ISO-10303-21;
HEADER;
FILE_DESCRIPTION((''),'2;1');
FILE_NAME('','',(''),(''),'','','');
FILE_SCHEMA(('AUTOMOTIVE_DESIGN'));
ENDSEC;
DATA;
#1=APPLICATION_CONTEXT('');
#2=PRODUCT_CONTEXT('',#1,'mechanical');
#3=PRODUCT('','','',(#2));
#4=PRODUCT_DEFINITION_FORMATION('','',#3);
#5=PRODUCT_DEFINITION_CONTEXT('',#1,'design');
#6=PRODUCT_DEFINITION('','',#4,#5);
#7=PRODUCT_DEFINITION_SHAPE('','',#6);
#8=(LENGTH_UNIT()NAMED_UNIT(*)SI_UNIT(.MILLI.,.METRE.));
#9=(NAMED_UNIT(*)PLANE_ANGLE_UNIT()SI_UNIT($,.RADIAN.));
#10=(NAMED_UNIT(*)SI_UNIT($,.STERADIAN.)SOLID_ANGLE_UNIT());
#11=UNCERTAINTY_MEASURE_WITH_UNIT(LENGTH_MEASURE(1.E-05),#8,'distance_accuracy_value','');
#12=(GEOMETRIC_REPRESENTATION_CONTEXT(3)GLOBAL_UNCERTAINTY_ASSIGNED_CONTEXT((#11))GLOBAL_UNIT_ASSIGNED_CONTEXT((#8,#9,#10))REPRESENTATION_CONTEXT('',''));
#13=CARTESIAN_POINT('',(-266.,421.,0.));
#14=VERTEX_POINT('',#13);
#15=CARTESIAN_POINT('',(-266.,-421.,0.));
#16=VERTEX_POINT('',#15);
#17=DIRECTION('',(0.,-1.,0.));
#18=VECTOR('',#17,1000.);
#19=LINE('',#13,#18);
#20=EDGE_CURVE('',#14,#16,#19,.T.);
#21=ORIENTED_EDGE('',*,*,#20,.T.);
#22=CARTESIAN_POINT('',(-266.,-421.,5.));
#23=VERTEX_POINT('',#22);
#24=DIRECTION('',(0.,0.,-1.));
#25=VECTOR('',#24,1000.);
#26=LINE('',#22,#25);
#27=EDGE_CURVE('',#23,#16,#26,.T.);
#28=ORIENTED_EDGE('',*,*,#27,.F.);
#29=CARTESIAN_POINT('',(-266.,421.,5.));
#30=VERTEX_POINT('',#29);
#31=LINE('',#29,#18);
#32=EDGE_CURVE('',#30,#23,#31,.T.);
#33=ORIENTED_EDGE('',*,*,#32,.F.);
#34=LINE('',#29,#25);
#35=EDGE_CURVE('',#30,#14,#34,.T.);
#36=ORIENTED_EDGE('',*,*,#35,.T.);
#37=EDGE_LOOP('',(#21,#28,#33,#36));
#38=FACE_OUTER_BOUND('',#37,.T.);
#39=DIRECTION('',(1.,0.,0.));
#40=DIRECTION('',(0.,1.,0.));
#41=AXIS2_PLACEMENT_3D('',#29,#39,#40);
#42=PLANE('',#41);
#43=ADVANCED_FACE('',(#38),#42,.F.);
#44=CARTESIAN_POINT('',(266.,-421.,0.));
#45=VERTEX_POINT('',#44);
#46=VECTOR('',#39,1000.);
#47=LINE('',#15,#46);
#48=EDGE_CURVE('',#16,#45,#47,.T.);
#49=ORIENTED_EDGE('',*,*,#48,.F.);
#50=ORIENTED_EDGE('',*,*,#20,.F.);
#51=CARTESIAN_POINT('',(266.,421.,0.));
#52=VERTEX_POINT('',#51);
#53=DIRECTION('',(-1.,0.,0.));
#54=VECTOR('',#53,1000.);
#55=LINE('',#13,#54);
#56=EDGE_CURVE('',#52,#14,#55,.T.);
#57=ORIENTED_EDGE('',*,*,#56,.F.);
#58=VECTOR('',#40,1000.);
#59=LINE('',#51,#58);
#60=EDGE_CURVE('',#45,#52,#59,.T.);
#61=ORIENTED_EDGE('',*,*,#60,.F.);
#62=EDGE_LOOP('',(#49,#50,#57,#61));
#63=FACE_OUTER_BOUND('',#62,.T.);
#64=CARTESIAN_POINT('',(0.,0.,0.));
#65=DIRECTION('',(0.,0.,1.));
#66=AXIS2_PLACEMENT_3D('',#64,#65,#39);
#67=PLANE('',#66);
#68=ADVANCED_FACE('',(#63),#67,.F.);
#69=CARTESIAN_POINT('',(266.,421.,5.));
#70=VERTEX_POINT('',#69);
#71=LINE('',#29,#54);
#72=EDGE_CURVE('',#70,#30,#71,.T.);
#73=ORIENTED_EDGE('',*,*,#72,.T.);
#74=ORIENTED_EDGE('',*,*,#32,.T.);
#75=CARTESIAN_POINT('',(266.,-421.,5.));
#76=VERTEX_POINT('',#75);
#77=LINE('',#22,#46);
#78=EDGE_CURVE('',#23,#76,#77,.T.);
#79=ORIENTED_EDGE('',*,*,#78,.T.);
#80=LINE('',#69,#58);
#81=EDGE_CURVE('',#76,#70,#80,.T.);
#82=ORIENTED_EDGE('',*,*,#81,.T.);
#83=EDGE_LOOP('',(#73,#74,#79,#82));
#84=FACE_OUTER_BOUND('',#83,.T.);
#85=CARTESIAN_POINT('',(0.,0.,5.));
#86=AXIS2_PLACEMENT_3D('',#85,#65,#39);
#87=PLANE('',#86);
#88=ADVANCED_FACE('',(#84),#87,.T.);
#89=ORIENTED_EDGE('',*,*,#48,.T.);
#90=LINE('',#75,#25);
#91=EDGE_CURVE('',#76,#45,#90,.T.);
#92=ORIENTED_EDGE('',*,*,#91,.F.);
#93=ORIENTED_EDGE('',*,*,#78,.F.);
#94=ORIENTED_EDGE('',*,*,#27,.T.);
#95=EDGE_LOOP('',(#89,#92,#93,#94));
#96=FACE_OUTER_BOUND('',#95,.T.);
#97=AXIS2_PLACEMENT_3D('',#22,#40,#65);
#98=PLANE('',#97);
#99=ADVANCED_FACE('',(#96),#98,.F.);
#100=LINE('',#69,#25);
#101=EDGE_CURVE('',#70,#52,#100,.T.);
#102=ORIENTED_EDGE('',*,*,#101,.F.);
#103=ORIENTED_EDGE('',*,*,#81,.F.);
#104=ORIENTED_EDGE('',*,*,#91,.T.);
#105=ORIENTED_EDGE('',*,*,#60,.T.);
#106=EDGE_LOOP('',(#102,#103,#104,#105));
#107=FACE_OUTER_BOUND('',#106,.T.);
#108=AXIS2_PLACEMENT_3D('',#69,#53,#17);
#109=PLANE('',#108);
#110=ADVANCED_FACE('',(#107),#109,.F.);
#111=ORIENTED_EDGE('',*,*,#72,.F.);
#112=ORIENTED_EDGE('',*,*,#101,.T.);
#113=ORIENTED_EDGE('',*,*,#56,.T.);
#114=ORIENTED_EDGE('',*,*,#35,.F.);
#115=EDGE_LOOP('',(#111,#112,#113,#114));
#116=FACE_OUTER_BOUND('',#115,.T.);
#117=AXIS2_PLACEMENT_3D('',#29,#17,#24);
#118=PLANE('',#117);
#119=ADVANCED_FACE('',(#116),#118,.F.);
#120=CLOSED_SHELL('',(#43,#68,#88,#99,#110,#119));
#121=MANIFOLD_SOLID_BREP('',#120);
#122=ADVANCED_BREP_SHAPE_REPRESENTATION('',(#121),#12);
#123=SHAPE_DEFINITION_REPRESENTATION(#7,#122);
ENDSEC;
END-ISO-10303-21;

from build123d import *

# Parameters (mm, degrees)
SKETCH_1_W      = 532
SKETCH_1_H      = 842
EXTRUDE_1_DEPTH = 5


with BuildPart() as part:
    # 草图1 → 凸台-拉伸1 (new body)
    with BuildSketch(Plane.XY):
        Rectangle(SKETCH_1_W, SKETCH_1_H)
    extrude(amount=EXTRUDE_1_DEPTH)


solid = part.part
